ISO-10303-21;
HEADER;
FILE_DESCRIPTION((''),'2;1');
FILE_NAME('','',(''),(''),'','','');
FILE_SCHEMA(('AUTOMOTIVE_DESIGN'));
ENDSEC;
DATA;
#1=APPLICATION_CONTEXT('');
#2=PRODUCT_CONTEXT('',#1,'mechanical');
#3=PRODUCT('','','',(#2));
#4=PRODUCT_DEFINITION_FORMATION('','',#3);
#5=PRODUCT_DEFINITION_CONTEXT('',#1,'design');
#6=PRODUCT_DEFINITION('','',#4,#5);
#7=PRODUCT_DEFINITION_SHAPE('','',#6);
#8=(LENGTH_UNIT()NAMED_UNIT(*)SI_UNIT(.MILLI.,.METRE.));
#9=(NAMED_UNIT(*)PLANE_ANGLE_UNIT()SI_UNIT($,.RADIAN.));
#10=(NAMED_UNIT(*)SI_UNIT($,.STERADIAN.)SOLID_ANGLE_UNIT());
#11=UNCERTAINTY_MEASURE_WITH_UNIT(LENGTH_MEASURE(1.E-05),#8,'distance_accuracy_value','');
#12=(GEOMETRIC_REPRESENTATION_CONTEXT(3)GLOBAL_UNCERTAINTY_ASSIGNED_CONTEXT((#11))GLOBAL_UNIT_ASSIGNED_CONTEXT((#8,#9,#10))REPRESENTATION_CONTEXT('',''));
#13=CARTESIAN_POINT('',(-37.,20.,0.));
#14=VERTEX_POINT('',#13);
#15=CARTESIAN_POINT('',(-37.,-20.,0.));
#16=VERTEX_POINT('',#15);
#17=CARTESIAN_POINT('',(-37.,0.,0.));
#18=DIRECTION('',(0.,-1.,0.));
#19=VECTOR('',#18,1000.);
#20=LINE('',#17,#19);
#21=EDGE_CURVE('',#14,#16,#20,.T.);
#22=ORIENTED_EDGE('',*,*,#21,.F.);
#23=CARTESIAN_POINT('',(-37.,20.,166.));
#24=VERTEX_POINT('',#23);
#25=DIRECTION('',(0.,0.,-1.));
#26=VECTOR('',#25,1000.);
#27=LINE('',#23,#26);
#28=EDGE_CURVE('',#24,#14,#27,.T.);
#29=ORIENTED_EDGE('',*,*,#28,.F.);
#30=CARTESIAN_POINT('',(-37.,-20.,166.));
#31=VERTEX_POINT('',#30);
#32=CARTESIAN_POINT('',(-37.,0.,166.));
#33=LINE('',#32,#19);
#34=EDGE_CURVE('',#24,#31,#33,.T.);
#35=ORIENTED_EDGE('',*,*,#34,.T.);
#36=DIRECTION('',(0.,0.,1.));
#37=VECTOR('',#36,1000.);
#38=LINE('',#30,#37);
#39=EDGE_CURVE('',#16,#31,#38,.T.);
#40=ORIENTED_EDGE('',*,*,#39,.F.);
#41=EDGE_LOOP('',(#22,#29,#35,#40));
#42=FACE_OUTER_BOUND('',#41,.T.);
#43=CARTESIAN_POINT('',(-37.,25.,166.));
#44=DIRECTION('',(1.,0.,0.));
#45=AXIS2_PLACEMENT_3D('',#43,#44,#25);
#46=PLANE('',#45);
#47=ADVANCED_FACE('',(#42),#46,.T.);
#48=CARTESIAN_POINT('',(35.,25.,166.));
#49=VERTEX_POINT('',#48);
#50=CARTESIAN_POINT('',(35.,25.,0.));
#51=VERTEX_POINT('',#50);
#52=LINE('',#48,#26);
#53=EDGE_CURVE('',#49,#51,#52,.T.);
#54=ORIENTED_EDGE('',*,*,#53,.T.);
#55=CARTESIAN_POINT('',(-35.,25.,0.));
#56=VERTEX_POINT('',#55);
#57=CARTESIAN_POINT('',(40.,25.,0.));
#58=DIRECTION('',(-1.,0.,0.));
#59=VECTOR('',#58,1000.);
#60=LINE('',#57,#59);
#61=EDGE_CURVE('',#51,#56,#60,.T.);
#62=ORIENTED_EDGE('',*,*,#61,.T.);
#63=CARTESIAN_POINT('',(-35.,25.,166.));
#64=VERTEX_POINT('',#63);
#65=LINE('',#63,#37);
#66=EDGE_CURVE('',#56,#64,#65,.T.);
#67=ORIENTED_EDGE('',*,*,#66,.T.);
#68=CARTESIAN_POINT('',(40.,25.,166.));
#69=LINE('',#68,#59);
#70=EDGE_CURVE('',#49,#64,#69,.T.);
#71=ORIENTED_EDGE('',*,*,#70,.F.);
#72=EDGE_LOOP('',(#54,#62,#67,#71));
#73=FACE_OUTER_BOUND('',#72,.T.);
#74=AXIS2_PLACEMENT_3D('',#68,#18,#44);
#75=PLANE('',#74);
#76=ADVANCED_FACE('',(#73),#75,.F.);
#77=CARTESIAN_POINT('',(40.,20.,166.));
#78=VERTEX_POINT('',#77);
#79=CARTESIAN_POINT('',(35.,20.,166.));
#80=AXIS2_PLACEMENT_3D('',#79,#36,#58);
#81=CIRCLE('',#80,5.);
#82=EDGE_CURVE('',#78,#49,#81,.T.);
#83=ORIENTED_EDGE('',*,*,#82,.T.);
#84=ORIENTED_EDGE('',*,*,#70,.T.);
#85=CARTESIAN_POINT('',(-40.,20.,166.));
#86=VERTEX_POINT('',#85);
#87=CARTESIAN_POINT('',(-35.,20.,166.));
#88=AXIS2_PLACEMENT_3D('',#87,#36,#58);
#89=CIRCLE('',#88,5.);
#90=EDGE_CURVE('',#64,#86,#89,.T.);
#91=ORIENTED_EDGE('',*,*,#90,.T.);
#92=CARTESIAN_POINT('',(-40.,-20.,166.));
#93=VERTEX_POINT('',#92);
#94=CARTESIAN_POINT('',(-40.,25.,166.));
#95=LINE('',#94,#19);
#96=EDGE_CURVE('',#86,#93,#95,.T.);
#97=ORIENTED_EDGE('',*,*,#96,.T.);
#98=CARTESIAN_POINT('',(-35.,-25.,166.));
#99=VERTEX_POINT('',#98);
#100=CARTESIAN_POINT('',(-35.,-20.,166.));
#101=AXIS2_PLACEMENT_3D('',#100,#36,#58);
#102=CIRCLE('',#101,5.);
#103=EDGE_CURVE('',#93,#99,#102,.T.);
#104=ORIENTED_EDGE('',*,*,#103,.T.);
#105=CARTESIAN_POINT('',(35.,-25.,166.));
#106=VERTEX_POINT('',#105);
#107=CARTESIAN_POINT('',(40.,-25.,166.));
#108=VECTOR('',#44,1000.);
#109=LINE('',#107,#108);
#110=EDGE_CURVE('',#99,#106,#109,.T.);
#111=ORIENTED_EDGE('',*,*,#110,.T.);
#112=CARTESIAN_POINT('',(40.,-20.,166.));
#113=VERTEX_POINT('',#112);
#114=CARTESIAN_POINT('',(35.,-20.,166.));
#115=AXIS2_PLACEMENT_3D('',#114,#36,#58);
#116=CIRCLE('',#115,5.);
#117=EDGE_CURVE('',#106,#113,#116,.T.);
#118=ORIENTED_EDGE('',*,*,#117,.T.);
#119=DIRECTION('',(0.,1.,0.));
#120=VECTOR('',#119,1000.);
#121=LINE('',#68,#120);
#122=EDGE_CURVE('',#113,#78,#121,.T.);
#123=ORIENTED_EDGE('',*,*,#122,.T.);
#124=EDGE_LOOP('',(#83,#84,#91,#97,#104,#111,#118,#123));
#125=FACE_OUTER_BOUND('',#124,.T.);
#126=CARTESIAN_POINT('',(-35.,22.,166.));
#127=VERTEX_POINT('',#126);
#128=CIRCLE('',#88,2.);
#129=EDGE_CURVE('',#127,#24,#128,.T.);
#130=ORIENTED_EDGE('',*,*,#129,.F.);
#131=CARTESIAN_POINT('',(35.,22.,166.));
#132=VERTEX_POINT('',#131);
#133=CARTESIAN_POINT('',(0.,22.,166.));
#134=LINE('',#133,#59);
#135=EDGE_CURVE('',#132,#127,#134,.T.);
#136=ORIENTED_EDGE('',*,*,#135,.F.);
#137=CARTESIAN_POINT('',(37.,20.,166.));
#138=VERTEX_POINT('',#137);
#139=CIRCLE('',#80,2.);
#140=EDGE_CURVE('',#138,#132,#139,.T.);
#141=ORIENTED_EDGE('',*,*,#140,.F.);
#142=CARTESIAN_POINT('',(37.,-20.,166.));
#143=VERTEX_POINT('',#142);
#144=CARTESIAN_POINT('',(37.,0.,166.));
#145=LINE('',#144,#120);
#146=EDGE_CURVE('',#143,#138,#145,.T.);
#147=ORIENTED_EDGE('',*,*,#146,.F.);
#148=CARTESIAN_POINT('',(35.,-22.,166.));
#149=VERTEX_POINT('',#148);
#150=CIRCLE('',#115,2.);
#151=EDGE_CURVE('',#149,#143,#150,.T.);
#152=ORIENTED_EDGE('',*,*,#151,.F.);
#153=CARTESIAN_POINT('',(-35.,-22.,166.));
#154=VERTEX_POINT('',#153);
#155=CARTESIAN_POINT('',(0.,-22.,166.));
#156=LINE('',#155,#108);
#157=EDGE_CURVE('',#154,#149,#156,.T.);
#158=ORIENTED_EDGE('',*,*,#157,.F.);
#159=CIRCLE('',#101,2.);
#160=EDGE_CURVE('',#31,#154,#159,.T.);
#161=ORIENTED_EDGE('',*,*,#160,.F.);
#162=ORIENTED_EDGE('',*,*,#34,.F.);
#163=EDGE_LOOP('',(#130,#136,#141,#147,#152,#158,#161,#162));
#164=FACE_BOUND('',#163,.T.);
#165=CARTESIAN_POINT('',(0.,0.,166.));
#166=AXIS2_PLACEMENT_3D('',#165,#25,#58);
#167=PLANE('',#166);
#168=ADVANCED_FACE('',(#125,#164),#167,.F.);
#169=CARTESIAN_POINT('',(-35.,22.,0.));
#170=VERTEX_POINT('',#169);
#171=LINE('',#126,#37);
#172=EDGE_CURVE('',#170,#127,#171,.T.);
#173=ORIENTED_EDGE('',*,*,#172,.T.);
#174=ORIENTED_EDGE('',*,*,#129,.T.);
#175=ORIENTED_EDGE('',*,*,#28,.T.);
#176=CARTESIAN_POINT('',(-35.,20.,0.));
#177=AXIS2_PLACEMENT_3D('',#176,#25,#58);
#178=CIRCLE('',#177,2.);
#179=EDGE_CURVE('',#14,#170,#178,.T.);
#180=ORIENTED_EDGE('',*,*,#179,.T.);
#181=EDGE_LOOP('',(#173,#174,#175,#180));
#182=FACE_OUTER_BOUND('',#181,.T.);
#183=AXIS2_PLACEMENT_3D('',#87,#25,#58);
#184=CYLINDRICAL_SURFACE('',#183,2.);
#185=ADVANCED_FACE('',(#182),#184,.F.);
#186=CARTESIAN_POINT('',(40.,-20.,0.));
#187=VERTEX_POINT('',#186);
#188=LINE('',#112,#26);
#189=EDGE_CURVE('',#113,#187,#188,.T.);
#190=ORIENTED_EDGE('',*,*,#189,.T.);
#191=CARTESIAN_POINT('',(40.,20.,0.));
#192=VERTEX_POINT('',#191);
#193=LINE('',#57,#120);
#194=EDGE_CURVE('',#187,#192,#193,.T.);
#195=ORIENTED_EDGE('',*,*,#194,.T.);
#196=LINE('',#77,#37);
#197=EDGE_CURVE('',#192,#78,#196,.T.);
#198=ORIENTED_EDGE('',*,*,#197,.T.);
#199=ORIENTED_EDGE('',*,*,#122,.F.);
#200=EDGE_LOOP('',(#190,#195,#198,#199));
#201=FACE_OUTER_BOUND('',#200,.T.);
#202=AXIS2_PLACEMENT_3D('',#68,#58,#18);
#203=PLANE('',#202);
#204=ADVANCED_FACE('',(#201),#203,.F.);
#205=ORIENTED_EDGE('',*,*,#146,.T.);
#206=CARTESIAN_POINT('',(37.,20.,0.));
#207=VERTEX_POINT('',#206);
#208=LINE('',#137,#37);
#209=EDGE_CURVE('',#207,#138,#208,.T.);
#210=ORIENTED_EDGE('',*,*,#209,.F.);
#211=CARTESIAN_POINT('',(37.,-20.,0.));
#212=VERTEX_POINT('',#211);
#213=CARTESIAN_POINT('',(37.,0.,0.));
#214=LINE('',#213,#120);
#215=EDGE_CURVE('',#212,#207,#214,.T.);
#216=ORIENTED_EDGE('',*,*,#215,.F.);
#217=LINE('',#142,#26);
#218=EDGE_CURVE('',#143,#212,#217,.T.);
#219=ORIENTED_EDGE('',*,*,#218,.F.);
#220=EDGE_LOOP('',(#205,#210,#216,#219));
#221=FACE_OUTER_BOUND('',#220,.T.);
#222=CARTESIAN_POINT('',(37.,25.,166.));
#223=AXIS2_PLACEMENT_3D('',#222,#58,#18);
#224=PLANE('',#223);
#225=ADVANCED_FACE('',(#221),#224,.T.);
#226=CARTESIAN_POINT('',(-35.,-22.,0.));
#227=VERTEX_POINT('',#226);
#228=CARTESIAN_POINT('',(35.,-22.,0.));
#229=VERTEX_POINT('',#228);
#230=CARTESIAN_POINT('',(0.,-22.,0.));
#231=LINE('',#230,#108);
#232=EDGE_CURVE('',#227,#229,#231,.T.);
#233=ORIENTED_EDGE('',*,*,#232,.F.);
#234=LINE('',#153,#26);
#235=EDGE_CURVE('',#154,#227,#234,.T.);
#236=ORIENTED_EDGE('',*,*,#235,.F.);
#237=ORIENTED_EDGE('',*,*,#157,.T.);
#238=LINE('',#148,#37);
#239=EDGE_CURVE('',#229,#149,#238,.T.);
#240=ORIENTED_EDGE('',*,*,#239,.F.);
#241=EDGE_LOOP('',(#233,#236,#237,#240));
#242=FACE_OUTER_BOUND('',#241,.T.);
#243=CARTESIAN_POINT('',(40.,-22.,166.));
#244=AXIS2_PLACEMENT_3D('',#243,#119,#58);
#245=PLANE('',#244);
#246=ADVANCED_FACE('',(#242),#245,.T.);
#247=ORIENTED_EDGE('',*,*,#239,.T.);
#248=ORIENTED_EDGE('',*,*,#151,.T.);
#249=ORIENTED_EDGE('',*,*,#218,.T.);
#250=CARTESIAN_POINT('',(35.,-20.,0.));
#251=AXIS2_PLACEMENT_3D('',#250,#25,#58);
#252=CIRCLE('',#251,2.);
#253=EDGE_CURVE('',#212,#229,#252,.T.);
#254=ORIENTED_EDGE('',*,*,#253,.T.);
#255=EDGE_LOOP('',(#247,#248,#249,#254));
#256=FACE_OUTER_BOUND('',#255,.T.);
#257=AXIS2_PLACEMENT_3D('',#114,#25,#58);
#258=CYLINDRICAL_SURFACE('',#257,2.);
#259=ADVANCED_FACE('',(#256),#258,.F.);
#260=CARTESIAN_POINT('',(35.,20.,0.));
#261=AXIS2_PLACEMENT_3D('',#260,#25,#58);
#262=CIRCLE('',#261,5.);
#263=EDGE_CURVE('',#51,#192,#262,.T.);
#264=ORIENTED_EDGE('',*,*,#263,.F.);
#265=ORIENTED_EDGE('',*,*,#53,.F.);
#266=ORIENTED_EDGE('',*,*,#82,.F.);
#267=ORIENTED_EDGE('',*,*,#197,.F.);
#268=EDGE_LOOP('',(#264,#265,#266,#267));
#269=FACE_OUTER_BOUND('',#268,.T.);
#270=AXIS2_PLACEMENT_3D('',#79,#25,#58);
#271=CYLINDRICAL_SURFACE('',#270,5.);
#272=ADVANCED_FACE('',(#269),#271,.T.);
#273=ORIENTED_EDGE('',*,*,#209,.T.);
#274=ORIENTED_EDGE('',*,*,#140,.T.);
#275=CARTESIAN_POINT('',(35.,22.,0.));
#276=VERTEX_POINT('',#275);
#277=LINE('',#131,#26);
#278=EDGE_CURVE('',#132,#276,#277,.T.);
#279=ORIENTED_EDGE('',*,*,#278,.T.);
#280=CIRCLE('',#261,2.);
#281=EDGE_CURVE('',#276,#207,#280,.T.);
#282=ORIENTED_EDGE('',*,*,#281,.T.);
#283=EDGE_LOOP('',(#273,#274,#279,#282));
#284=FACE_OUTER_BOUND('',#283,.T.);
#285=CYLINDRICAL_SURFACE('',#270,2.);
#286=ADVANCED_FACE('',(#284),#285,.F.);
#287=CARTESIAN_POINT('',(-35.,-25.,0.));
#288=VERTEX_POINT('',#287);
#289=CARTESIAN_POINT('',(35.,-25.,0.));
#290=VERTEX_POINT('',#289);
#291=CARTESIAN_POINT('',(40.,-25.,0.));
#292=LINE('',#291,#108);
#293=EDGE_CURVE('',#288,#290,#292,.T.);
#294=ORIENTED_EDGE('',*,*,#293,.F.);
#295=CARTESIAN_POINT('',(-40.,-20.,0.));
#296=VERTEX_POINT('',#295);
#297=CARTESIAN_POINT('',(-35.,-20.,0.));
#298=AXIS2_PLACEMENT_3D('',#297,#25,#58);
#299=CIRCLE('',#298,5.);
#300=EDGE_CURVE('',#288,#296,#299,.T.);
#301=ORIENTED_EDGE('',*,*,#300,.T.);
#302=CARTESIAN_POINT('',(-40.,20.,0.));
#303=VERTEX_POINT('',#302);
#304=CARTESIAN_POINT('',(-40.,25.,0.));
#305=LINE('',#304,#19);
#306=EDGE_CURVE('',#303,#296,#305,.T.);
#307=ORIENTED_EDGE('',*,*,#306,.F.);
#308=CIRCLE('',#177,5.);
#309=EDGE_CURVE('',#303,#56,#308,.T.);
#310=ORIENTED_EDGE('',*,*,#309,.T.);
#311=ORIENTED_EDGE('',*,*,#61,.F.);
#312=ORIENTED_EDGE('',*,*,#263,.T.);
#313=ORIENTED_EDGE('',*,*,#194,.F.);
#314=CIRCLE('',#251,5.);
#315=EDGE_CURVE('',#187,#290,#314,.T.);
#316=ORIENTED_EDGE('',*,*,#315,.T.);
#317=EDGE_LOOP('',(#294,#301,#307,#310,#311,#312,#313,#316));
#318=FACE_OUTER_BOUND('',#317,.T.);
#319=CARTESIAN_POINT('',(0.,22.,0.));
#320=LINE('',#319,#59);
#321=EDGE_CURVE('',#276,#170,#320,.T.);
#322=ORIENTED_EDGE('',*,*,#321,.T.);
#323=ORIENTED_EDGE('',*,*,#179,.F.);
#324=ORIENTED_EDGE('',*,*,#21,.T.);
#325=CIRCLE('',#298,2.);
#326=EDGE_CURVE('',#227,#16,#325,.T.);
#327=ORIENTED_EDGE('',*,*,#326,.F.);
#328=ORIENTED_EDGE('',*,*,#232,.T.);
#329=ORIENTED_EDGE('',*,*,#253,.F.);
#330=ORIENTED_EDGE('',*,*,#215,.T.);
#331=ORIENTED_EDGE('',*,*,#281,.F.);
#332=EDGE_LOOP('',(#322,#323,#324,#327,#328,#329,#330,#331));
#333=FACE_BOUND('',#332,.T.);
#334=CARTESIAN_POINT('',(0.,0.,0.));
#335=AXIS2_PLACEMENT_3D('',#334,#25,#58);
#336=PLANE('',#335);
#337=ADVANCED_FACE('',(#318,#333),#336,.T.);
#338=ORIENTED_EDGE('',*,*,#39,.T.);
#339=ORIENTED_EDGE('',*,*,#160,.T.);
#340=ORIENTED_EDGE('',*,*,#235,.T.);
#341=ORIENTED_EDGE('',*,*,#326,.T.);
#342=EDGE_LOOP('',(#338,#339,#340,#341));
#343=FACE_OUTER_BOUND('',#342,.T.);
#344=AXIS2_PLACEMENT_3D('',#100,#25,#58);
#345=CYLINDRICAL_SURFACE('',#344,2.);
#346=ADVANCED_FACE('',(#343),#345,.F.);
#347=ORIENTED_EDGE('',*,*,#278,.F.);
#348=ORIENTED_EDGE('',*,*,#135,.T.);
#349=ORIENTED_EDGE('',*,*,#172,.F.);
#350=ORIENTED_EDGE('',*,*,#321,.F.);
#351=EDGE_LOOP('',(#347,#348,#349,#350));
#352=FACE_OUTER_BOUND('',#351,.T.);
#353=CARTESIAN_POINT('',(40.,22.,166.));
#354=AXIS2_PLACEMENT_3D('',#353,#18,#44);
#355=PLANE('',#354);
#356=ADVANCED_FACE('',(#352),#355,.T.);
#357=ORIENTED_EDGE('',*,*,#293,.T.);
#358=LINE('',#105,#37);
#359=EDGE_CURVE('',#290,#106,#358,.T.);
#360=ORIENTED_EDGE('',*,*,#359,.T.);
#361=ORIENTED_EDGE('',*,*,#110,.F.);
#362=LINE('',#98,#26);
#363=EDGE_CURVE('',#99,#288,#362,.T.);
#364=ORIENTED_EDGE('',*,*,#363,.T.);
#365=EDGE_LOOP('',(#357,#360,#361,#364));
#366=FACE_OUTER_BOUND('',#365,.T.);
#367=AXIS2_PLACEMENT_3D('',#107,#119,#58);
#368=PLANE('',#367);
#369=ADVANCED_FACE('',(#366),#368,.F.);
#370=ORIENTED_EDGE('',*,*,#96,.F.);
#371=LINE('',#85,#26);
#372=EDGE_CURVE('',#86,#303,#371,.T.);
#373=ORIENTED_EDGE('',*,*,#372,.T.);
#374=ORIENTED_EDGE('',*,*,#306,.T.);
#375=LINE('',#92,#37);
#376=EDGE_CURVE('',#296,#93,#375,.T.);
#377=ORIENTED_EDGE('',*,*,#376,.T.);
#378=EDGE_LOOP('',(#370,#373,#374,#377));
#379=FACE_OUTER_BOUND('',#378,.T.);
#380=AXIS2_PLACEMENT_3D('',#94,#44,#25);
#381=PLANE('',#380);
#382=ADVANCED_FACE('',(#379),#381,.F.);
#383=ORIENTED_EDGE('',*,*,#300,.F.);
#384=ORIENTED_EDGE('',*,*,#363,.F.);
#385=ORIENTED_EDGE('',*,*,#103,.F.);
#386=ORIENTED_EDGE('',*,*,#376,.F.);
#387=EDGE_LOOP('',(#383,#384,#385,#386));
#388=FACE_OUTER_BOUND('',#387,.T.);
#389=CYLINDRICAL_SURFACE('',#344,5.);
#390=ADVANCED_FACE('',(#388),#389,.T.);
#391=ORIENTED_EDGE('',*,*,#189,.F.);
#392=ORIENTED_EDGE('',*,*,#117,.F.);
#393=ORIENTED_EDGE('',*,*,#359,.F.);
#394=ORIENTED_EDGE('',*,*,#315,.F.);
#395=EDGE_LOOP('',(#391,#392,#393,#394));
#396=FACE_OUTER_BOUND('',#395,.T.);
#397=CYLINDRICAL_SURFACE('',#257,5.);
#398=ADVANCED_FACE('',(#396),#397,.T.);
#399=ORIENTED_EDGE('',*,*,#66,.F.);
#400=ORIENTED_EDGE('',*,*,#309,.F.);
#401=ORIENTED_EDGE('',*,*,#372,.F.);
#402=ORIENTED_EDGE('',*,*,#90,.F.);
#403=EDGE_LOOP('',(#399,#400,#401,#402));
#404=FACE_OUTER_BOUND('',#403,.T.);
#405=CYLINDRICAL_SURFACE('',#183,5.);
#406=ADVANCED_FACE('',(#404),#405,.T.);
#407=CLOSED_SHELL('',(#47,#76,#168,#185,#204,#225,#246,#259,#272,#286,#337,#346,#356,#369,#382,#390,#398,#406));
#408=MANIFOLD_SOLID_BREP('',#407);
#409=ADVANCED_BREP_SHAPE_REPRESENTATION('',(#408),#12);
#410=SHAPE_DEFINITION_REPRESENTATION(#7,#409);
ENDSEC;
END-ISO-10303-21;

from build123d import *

# Parameters (mm, degrees)
SKETCH1_W           = 80
SKETCH1_H           = 50
BOSS_EXTRUDE1_DEPTH = 166
FILLET1_R           = 5
SHELL1_T            = -3


with BuildPart() as part:
    # Sketch1 → Boss-Extrude1 (new body)
    with BuildSketch(Plane.XY):
        Rectangle(SKETCH1_W, SKETCH1_H)
    extrude(amount=BOSS_EXTRUDE1_DEPTH)

    # Fillet1
    fillet1_edges = [part.edges().sort_by_distance(p)[0] for p in [
        (-40, 25, 83),
        (40, 25, 83),
        (40, -25, 83),
        (-40, -25, 83),
    ]]
    fillet(fillet1_edges, radius=FILLET1_R)

    # Shell1
    shell1_openings = [part.faces().sort_by_distance(p)[0] for p in [
        (0, 0, 166),
        (0, 0, 0),
    ]]
    offset(amount=SHELL1_T, openings=shell1_openings, kind=Kind.INTERSECTION)


solid = part.part
